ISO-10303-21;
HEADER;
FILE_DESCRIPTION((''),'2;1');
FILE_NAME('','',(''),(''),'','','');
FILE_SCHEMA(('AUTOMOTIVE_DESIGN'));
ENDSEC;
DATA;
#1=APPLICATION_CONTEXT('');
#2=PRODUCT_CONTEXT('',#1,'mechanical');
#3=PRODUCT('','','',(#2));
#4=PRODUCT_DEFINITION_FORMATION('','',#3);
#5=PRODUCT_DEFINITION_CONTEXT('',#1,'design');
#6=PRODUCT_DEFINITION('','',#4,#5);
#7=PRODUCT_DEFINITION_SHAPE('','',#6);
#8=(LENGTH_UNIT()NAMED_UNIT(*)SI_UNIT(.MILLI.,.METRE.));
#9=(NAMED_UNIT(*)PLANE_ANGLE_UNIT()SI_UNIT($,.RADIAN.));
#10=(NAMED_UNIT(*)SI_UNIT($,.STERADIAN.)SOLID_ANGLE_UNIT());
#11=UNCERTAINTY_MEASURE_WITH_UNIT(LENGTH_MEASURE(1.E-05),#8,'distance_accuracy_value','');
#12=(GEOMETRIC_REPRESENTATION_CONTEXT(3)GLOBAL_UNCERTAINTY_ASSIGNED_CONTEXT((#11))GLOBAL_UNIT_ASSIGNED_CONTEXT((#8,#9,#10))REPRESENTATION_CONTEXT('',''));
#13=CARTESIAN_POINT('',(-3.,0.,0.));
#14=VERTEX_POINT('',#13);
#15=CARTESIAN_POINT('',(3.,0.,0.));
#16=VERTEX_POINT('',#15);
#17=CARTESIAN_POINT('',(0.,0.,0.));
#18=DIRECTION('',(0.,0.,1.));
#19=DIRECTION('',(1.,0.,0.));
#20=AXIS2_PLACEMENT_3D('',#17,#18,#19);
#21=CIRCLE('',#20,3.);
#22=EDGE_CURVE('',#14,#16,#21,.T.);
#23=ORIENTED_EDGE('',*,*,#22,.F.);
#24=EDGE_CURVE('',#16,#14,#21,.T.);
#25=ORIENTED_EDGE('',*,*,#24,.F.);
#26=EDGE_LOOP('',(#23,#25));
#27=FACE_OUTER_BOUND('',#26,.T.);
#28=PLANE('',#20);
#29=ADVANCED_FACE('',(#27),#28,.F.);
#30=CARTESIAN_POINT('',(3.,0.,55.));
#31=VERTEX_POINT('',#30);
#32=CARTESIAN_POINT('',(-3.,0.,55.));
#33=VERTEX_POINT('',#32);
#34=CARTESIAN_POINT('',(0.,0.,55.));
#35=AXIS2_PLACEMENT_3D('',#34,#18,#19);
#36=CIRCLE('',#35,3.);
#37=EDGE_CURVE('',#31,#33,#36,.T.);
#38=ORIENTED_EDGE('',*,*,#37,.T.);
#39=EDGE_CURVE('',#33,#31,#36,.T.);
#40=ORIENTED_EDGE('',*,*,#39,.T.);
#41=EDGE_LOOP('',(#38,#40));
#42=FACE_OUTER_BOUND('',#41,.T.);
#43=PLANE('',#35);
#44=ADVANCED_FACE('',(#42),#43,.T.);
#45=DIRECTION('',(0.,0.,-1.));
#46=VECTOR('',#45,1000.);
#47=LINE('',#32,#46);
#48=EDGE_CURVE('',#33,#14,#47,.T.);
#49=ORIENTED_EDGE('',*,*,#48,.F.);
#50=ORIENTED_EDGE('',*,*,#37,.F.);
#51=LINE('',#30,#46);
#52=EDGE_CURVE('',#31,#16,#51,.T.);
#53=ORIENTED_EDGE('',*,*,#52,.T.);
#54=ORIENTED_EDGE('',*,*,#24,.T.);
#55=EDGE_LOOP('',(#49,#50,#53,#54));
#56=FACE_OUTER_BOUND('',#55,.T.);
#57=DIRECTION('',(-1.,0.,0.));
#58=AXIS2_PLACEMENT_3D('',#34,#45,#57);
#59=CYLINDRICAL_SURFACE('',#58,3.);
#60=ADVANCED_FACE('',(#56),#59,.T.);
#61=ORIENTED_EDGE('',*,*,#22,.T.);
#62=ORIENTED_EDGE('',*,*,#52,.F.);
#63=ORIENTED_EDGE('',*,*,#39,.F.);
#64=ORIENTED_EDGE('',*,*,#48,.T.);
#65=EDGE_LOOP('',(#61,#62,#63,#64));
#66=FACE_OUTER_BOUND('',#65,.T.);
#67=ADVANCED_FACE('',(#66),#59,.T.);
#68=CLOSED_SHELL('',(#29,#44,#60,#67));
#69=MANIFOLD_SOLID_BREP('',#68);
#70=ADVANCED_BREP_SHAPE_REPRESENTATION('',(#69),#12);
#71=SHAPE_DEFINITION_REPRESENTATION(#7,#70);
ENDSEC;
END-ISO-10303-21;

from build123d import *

# Parameters (mm, degrees)
SKETCH_1_R      = 3
EXTRUDE_2_DEPTH = 55


with BuildPart() as part:
    # 草图1 → 凸台-拉伸2 (new body)
    with BuildSketch(Plane.XY):
        Circle(SKETCH_1_R)
    extrude(amount=EXTRUDE_2_DEPTH)


solid = part.part
